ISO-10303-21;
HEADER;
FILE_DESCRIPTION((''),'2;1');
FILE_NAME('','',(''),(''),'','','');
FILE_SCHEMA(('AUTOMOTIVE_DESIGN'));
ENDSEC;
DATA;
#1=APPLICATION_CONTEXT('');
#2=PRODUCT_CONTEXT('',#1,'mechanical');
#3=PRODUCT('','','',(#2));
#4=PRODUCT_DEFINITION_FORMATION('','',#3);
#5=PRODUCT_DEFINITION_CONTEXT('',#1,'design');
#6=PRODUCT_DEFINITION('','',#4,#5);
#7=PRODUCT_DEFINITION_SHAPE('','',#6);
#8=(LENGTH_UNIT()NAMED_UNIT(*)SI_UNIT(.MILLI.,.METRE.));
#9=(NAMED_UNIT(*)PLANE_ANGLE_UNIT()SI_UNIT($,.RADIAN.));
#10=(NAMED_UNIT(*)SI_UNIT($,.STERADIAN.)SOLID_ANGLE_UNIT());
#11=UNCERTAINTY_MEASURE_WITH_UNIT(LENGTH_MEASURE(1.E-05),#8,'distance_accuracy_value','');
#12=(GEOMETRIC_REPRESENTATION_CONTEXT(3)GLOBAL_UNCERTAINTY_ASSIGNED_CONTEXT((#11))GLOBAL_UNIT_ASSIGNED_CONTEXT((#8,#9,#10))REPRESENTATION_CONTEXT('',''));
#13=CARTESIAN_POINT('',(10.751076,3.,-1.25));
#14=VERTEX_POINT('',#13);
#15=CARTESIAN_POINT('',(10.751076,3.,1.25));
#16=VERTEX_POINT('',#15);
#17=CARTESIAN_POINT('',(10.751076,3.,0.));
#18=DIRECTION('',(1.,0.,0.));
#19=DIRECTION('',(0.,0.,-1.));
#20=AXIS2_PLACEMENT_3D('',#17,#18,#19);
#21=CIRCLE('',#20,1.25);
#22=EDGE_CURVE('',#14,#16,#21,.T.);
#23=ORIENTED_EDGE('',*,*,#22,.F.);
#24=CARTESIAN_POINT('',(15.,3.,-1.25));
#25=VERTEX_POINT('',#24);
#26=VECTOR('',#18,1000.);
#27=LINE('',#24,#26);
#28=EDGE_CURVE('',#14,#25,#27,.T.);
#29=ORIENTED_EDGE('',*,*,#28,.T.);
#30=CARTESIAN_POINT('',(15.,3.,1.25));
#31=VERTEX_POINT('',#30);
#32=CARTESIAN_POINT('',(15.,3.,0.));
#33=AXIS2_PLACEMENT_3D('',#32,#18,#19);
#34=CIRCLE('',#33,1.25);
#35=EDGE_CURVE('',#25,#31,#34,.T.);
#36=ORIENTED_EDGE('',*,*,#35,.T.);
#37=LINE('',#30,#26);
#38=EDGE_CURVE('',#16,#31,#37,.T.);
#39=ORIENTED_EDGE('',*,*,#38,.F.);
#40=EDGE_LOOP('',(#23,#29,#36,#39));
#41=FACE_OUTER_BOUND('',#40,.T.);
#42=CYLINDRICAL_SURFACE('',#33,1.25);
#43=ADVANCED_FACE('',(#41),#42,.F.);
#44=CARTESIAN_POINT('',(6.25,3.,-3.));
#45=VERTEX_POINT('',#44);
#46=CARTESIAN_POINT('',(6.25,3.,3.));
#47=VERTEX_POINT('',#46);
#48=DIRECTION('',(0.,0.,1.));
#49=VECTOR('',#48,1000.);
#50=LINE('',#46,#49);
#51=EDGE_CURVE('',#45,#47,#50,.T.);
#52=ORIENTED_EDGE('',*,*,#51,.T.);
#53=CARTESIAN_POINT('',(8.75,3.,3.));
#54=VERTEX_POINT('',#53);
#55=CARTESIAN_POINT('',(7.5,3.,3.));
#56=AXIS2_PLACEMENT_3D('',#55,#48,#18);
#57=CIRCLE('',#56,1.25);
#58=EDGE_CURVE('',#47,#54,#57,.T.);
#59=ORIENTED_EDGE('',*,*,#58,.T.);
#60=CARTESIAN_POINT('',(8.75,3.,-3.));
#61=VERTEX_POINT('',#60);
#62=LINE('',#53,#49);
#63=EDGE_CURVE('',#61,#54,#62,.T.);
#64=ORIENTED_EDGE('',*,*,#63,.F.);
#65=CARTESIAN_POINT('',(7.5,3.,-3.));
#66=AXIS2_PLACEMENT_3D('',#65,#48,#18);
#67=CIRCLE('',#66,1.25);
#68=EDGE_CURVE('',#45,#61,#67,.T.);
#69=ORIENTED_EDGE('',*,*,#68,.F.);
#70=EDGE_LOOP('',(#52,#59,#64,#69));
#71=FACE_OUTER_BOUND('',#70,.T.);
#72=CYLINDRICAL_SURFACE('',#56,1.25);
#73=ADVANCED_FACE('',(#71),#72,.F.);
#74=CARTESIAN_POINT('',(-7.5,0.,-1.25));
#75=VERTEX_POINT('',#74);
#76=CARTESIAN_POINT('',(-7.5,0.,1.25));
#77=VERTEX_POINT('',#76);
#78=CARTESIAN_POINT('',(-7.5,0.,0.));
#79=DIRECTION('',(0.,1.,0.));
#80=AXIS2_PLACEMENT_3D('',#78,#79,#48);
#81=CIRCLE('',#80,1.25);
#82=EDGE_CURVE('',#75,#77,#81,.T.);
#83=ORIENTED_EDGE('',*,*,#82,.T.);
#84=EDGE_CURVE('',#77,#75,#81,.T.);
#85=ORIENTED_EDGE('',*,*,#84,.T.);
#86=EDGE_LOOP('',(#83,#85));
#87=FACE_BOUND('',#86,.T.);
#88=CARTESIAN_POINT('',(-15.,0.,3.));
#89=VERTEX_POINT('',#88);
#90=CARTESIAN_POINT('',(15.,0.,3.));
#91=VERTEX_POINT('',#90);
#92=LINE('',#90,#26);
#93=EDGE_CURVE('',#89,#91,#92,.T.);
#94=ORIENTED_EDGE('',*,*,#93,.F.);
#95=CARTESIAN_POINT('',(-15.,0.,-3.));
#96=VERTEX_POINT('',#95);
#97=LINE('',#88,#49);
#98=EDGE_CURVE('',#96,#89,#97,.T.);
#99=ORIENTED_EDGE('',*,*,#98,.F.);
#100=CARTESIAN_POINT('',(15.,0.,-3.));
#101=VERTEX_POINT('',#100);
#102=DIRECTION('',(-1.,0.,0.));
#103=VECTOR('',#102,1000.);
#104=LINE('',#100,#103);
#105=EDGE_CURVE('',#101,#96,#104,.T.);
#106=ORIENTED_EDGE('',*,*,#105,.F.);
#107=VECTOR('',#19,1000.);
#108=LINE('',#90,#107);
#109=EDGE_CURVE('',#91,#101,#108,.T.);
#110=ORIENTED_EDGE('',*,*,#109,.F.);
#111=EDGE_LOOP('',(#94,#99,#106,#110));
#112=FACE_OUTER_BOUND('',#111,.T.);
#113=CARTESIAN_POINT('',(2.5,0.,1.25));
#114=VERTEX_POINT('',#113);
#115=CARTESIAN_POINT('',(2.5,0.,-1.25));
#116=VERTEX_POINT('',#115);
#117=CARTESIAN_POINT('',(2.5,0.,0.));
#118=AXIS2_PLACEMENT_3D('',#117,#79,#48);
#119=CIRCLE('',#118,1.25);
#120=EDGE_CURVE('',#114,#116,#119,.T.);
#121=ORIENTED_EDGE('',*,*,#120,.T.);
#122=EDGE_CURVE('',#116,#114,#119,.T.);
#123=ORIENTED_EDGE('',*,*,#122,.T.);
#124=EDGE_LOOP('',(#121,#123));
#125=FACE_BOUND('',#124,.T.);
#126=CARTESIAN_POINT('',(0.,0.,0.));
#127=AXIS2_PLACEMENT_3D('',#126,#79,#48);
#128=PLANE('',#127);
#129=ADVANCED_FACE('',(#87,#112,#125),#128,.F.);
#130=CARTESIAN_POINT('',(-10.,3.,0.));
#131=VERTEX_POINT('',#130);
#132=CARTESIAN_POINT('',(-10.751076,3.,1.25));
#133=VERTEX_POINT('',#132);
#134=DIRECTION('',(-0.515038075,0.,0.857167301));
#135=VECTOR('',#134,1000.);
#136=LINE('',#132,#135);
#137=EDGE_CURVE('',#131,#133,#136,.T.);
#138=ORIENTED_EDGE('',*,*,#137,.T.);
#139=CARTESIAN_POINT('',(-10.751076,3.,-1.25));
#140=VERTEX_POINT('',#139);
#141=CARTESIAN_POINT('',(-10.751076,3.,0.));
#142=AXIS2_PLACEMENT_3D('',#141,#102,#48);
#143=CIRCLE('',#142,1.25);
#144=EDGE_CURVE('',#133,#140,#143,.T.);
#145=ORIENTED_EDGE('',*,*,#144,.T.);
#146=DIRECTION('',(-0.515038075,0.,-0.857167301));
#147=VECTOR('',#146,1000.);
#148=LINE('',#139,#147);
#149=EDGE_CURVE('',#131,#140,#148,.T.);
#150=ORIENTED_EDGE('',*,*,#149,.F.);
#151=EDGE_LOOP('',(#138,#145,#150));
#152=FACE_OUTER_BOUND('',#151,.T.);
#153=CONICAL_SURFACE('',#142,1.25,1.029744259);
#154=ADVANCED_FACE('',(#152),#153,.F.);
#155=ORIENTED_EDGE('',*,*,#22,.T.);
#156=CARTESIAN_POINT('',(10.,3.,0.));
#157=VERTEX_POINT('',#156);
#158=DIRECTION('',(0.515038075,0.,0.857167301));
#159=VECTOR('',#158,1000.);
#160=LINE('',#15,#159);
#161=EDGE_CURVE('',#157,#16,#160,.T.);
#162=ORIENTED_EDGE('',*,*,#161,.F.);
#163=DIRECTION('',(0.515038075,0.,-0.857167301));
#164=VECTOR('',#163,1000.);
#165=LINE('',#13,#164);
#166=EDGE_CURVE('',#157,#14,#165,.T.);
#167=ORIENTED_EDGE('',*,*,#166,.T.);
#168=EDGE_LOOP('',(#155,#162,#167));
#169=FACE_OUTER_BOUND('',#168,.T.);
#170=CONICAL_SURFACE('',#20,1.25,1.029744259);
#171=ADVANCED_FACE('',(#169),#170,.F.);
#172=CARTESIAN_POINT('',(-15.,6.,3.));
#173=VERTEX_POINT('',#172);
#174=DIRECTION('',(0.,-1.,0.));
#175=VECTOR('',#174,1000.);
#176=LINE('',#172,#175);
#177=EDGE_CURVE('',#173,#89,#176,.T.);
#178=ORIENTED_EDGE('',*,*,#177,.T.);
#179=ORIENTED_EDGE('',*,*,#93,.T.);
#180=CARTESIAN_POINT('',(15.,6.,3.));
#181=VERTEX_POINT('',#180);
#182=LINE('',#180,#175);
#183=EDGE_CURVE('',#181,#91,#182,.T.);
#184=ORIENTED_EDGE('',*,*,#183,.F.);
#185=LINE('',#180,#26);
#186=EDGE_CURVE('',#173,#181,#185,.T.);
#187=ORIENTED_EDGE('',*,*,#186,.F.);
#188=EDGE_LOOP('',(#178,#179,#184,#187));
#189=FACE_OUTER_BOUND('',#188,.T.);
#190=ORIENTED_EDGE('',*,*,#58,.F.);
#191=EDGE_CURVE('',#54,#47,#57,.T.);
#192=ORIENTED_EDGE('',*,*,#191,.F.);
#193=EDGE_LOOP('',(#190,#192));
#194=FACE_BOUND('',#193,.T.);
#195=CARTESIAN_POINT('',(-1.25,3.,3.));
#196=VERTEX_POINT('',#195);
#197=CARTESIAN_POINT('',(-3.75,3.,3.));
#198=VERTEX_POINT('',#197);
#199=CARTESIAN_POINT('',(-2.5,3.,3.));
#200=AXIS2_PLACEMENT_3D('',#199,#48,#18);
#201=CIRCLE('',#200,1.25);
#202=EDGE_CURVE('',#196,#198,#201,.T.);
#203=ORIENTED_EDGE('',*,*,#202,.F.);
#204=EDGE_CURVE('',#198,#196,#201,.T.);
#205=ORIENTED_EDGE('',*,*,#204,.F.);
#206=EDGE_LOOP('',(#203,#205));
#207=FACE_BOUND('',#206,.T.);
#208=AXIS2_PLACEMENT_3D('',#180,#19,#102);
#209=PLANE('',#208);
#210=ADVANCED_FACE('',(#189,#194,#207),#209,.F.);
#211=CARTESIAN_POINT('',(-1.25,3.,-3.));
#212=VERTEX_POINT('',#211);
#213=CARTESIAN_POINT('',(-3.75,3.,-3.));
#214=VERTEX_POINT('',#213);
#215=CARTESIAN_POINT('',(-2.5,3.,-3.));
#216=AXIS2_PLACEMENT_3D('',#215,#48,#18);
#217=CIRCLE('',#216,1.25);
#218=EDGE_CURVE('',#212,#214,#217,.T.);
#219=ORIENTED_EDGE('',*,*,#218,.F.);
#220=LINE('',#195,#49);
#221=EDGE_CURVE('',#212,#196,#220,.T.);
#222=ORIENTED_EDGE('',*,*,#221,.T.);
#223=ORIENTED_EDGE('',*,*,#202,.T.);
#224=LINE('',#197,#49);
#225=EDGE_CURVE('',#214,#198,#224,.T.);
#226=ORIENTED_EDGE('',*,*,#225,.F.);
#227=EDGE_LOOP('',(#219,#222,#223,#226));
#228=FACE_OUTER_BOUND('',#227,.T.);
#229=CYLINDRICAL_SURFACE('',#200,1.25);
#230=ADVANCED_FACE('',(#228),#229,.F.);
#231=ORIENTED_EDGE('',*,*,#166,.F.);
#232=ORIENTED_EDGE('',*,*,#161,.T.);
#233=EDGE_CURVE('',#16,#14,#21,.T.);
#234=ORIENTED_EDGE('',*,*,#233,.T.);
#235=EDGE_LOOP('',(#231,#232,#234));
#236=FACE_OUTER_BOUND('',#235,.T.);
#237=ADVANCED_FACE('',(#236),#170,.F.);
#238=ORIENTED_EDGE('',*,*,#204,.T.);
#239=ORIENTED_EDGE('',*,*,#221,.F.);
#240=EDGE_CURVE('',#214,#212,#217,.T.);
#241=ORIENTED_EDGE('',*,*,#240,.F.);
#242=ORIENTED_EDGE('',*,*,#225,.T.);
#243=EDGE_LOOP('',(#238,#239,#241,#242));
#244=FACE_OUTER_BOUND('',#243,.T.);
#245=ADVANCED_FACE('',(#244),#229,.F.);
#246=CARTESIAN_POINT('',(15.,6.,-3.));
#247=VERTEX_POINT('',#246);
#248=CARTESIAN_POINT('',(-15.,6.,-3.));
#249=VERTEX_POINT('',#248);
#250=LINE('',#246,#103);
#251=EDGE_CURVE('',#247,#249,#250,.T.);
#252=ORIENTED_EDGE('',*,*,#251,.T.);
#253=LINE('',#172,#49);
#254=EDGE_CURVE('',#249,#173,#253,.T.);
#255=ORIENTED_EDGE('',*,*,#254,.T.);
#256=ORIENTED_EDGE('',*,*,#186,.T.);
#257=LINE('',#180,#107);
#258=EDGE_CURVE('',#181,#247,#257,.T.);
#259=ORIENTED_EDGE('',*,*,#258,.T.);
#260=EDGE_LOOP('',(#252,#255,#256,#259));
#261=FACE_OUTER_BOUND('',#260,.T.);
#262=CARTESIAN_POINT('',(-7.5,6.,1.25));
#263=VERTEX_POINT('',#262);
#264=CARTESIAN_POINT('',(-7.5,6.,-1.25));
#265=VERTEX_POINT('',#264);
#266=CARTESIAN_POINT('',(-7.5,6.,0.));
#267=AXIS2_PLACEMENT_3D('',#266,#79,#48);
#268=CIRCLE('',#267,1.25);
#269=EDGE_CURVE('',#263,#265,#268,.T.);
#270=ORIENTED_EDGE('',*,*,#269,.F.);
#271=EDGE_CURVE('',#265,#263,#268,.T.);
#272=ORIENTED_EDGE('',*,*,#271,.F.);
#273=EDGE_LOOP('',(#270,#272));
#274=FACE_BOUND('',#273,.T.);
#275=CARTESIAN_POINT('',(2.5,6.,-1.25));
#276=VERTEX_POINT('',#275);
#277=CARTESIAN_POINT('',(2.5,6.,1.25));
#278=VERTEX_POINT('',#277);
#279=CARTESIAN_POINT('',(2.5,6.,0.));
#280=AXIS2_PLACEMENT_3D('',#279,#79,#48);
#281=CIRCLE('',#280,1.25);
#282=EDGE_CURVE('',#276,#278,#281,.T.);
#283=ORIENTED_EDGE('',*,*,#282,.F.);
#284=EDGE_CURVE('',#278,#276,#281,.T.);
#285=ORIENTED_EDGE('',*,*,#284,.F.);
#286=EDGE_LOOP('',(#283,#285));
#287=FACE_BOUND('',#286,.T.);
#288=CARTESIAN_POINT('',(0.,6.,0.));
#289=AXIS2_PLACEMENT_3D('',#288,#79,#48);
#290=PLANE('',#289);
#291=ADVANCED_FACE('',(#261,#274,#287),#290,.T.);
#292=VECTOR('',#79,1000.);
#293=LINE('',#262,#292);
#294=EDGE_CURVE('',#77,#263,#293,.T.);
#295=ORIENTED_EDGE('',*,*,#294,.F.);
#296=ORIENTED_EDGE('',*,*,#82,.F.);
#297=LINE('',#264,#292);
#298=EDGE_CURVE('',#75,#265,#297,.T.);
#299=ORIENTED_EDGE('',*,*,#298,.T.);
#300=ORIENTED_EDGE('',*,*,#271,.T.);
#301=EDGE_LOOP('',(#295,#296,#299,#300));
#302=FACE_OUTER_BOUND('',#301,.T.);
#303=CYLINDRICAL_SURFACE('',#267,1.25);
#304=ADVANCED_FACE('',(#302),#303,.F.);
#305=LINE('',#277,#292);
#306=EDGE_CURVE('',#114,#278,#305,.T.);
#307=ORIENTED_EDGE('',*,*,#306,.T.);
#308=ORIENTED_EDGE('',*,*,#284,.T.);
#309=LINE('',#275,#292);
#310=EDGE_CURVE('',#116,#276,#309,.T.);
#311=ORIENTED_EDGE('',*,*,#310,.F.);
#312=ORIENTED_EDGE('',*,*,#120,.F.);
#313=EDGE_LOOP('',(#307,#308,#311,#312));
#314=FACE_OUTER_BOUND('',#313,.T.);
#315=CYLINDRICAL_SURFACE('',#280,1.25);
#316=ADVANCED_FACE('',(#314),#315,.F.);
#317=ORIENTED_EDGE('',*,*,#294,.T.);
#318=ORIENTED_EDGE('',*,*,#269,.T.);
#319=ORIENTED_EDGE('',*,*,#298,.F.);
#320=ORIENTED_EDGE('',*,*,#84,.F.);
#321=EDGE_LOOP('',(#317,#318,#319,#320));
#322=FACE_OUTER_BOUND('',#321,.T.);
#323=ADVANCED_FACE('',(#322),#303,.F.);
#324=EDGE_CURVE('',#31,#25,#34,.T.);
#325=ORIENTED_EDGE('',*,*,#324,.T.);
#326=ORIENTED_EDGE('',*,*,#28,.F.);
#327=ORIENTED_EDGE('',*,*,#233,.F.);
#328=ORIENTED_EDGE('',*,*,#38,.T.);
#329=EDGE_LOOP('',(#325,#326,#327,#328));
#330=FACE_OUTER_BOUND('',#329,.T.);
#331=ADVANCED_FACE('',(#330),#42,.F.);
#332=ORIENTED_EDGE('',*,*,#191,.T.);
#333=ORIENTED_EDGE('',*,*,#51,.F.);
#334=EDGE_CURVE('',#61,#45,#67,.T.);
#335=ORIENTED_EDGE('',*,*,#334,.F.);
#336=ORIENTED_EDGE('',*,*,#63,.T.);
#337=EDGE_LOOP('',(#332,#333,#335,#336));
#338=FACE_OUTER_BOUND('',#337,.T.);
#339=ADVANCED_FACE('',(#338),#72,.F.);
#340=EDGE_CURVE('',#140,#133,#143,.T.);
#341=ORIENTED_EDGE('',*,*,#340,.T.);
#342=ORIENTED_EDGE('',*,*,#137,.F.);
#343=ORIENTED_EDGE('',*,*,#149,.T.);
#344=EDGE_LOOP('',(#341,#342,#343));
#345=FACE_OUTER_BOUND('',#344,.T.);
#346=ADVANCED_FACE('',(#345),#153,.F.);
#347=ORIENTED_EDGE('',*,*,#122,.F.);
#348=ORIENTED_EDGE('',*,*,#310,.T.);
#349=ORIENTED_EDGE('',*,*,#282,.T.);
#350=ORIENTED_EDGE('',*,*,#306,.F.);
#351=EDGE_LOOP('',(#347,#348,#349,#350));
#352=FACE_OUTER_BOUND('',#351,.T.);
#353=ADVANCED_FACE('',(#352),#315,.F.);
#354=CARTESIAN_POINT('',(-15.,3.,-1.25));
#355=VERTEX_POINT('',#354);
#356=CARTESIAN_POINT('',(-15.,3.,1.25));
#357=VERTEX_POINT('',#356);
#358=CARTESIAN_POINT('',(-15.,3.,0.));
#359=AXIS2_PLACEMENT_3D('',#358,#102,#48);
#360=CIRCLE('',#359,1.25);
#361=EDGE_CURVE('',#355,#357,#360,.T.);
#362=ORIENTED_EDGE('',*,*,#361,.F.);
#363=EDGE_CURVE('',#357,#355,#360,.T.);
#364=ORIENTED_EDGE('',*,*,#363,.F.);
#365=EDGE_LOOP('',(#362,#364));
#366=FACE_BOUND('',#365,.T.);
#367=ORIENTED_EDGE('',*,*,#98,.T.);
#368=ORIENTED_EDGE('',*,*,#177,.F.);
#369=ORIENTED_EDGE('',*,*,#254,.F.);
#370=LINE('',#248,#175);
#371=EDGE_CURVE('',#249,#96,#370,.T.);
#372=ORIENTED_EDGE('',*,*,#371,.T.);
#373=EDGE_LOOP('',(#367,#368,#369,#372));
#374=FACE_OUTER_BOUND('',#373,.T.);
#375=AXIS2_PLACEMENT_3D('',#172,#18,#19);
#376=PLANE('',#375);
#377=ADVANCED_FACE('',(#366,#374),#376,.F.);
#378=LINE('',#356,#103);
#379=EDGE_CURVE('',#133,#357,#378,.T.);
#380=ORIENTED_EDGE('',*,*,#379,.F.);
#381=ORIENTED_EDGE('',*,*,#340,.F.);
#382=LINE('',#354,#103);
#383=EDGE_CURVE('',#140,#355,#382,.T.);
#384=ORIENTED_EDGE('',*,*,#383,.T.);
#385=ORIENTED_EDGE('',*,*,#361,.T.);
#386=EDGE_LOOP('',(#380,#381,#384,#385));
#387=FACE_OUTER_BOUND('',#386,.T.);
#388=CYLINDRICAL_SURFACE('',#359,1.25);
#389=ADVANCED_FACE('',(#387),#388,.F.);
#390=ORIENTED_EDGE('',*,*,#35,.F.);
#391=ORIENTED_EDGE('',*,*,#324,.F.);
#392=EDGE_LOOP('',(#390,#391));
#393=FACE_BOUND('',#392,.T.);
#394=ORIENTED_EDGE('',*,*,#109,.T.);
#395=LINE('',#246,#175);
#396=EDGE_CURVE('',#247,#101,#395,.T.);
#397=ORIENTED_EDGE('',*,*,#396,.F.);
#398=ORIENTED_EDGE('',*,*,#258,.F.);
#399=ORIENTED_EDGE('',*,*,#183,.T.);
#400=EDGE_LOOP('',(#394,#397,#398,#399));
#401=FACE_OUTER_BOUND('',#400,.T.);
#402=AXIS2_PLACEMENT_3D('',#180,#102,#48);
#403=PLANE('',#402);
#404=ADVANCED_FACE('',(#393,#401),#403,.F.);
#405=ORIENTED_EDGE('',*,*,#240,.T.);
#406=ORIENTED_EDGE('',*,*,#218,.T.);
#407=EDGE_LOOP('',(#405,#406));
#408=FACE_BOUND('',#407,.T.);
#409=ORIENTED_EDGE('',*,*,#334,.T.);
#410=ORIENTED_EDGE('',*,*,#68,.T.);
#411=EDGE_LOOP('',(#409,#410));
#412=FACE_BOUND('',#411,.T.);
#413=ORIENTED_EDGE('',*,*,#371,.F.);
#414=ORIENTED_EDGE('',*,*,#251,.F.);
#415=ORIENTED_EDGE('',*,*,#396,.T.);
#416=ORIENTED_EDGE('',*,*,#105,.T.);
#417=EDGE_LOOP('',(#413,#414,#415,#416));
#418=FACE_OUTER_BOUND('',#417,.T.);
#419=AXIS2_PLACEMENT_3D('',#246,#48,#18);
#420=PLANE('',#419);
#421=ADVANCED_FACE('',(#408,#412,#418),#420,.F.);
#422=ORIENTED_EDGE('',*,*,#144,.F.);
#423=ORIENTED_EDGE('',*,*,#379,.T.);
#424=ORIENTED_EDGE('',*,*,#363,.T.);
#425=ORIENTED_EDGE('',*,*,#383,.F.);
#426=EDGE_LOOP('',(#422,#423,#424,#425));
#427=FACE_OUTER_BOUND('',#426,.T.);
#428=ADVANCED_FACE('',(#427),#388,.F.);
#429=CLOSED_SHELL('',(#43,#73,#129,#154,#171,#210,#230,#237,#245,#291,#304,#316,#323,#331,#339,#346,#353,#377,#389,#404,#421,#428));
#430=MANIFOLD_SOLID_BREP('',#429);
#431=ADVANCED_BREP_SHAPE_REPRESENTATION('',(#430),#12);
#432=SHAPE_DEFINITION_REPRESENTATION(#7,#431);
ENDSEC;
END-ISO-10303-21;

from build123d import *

# Parameters (mm, degrees)
SKETCH_1_W             = 30
SKETCH_1_H             = 6
EXTRUDE_1_DEPTH        = 6
HOLE_WIZARD_M3_1_D     = 2.5
HOLE_WIZARD_M3_2_D     = 2.5
HOLE_WIZARD_M3_3_D     = 2.5
HOLE_WIZARD_M3_3_DEPTH = 4.248924226
HOLE_WIZARD_M3_3_TIP   = 0.751075774
HOLE_WIZARD_M3_4_D     = 2.5
HOLE_WIZARD_M3_4_DEPTH = 4.248924226
HOLE_WIZARD_M3_4_TIP   = 0.751075774


with BuildPart() as part:
    # 草图1 → 凸台-拉伸1 (new body)
    with BuildSketch(Plane(origin=(0, 0, 0), x_dir=(1, 0, 0), z_dir=(0, 1, 0))):
        Rectangle(SKETCH_1_W, SKETCH_1_H)
    extrude(amount=EXTRUDE_1_DEPTH)

    # M3 螺纹孔1 (through all)
    with Locations(Plane.XY.offset(3)):
        with Locations((-2.5, 3), (7.5, 3)):
            Hole(HOLE_WIZARD_M3_1_D / 2)

    # M3 螺纹孔2 (through all)
    with Locations(Plane(origin=(0, 6, 0), x_dir=(1, 0, 0), z_dir=(0, 1, 0))):
        with Locations((2.5, 0), (-7.5, 0)):
            Hole(HOLE_WIZARD_M3_2_D / 2)

    # M3 螺纹孔3
    with Locations(Plane.ZY.offset(15)):
        with Locations((0, 3)):
            Hole(HOLE_WIZARD_M3_3_D / 2, depth=HOLE_WIZARD_M3_3_DEPTH)
            with Locations((0, 0, -(HOLE_WIZARD_M3_3_DEPTH + HOLE_WIZARD_M3_3_TIP / 2))):  # 118° drill point
                Cone(0, HOLE_WIZARD_M3_3_D / 2, HOLE_WIZARD_M3_3_TIP, mode=Mode.SUBTRACT)

    # M3 螺纹孔4
    with Locations(Plane(origin=(15, 0, 0), x_dir=(0, 0, -1), z_dir=(1, 0, 0))):
        with Locations((0, 3)):
            Hole(HOLE_WIZARD_M3_4_D / 2, depth=HOLE_WIZARD_M3_4_DEPTH)
            with Locations((0, 0, -(HOLE_WIZARD_M3_4_DEPTH + HOLE_WIZARD_M3_4_TIP / 2))):  # 118° drill point
                Cone(0, HOLE_WIZARD_M3_4_D / 2, HOLE_WIZARD_M3_4_TIP, mode=Mode.SUBTRACT)


solid = part.part
